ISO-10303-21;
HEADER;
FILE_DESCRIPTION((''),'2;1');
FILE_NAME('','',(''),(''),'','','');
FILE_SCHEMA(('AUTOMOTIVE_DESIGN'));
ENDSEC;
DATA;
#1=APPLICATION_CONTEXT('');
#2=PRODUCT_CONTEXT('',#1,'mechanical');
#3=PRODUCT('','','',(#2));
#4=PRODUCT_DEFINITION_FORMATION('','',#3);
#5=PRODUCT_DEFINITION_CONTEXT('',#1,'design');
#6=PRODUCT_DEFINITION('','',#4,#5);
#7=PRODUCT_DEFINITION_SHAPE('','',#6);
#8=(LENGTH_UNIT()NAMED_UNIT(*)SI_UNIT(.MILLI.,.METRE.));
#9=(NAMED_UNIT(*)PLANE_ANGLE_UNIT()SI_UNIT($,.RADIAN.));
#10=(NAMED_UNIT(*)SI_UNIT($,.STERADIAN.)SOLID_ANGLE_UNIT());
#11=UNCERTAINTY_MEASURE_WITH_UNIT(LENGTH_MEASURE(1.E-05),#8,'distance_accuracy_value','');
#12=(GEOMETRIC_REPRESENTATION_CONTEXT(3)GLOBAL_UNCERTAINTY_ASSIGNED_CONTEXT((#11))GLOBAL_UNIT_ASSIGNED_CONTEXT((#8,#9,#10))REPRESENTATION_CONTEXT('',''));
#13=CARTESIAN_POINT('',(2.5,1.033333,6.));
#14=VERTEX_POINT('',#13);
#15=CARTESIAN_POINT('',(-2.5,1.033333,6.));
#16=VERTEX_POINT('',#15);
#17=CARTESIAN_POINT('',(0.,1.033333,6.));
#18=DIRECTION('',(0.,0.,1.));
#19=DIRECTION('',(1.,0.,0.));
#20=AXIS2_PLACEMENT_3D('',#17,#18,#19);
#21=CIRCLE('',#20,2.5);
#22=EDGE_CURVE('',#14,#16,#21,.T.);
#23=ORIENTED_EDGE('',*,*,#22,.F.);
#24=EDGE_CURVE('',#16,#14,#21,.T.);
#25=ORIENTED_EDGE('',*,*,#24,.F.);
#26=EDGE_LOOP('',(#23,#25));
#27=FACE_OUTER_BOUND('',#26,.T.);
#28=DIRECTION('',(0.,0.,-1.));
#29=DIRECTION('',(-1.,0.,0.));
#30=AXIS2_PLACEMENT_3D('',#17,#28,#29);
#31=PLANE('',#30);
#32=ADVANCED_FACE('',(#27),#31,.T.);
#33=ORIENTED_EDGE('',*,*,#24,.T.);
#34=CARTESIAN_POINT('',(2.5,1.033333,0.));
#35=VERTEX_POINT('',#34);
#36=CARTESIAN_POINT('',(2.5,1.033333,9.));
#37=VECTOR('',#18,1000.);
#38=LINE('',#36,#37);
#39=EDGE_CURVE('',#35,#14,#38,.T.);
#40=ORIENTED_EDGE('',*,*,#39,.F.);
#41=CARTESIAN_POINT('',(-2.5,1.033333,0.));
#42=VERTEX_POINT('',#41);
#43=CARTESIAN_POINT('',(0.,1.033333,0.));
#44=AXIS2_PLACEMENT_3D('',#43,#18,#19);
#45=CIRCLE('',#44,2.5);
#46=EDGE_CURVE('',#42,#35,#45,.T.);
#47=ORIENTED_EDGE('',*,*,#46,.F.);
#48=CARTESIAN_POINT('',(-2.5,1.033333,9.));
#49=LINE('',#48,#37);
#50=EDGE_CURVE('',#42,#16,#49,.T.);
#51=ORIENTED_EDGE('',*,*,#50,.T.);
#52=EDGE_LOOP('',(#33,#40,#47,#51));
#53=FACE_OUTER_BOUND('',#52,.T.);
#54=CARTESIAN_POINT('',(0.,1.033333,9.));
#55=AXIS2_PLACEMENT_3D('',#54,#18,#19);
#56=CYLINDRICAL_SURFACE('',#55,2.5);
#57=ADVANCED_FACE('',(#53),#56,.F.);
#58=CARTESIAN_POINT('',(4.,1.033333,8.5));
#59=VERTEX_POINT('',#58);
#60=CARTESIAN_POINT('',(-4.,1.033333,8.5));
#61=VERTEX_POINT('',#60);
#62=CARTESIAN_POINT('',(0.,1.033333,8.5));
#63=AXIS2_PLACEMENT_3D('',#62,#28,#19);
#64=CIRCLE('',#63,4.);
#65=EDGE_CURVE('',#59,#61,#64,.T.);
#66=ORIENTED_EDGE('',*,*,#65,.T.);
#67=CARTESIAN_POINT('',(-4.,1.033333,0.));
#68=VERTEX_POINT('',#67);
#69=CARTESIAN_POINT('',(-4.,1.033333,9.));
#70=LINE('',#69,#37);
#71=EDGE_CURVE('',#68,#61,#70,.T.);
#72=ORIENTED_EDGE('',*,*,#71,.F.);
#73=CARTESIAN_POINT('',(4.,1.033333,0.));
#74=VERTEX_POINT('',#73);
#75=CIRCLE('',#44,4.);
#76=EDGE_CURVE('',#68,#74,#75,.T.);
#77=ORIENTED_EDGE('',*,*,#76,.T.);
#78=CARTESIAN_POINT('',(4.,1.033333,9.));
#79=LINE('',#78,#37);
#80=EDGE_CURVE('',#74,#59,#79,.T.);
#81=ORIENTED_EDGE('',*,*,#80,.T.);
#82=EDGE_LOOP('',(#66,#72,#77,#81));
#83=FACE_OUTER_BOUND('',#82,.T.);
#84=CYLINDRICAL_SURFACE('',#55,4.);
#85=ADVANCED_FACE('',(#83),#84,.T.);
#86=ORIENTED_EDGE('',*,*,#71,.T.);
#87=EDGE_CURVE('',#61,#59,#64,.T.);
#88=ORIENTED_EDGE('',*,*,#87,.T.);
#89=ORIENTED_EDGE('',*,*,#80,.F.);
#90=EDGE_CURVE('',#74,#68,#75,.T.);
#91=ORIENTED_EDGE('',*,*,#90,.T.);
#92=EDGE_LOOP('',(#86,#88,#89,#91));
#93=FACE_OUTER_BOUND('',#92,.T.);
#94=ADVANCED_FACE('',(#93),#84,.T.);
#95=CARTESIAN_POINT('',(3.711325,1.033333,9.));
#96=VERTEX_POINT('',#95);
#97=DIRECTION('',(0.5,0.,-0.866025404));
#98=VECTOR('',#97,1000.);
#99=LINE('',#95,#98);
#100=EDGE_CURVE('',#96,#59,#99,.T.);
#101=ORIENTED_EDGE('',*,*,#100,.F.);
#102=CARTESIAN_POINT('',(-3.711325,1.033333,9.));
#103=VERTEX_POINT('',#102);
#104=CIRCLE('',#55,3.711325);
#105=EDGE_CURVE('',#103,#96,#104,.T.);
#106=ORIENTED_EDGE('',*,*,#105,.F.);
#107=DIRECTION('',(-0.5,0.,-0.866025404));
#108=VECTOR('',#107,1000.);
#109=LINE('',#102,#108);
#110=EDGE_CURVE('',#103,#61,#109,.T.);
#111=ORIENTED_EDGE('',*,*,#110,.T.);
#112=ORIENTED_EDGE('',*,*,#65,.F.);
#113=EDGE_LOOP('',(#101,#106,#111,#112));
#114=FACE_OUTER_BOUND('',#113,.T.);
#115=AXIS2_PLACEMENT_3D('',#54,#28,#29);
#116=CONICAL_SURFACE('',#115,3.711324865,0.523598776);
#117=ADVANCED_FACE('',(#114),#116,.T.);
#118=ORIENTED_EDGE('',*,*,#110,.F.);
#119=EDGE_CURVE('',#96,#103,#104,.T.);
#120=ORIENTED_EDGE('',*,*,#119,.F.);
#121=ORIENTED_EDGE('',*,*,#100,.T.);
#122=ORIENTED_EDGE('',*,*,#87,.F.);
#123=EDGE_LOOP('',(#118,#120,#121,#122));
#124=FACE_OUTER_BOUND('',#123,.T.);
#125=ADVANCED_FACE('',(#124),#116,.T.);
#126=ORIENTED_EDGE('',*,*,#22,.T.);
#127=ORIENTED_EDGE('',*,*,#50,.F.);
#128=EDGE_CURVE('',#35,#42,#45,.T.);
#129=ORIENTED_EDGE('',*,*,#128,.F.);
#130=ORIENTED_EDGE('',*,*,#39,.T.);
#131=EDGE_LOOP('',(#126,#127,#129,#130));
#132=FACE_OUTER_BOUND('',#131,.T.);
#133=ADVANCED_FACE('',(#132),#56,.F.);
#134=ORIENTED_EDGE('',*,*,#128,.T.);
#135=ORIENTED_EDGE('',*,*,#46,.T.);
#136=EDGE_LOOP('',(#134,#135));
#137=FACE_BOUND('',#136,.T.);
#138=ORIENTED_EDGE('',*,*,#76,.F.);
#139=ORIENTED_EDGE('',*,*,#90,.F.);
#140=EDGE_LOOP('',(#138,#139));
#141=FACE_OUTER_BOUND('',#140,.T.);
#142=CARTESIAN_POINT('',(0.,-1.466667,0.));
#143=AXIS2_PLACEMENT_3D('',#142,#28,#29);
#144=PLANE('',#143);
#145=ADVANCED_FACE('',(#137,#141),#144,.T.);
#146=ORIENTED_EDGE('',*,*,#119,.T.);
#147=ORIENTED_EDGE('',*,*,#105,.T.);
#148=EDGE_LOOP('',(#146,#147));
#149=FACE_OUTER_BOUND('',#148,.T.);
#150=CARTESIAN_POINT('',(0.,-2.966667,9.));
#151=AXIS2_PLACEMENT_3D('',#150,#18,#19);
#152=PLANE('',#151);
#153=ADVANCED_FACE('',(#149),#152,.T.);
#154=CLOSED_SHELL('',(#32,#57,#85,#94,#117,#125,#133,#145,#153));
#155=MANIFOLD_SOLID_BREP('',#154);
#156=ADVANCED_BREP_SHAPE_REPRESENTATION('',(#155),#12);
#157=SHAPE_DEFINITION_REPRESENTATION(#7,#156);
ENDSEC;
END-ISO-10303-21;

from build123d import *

# Parameters (mm, degrees)
END_CHAMFER_0_5X30DEG_SIZE  = 0.5
END_CHAMFER_0_5X30DEG_SIZE2 = 0.288675135


with BuildPart() as part:
    # Pin Profile Sketch → Pin Body Revolve (revolve)
    with BuildSketch(Plane(origin=(0, 0, 0), x_dir=(0, 0, -1), z_dir=(1, 0, 0)), mode=Mode.PRIVATE) as pin_body_revolve_sk:
        Polygon((0, -1.466666667), (0, -2.966666667), (-9, -2.966666667), (-9, 1.033333333), (-6, 1.033333333), (-6, -1.466666667), align=None)
    revolve(pin_body_revolve_sk.sketch.rotate(Axis((0, 1.033333333, 9), (0, 0, -1)), 270), axis=Axis((0, 1.033333333, 9), (0, 0, -1)))

    # End Chamfer 0.5x30deg
    end_chamfer_0_5x30deg_edges = [part.edges().sort_by_distance(p)[0] for p in [
        (-4, 1.033333333, 9),
    ]]
    end_chamfer_0_5x30deg_side = [part.faces().sort_by_distance(p)[0] for p in [
        (-4, 1.033333333, 4.5),
    ]]
    chamfer(end_chamfer_0_5x30deg_edges, length=END_CHAMFER_0_5X30DEG_SIZE, length2=END_CHAMFER_0_5X30DEG_SIZE2, reference=end_chamfer_0_5x30deg_side[0])


solid = part.part
